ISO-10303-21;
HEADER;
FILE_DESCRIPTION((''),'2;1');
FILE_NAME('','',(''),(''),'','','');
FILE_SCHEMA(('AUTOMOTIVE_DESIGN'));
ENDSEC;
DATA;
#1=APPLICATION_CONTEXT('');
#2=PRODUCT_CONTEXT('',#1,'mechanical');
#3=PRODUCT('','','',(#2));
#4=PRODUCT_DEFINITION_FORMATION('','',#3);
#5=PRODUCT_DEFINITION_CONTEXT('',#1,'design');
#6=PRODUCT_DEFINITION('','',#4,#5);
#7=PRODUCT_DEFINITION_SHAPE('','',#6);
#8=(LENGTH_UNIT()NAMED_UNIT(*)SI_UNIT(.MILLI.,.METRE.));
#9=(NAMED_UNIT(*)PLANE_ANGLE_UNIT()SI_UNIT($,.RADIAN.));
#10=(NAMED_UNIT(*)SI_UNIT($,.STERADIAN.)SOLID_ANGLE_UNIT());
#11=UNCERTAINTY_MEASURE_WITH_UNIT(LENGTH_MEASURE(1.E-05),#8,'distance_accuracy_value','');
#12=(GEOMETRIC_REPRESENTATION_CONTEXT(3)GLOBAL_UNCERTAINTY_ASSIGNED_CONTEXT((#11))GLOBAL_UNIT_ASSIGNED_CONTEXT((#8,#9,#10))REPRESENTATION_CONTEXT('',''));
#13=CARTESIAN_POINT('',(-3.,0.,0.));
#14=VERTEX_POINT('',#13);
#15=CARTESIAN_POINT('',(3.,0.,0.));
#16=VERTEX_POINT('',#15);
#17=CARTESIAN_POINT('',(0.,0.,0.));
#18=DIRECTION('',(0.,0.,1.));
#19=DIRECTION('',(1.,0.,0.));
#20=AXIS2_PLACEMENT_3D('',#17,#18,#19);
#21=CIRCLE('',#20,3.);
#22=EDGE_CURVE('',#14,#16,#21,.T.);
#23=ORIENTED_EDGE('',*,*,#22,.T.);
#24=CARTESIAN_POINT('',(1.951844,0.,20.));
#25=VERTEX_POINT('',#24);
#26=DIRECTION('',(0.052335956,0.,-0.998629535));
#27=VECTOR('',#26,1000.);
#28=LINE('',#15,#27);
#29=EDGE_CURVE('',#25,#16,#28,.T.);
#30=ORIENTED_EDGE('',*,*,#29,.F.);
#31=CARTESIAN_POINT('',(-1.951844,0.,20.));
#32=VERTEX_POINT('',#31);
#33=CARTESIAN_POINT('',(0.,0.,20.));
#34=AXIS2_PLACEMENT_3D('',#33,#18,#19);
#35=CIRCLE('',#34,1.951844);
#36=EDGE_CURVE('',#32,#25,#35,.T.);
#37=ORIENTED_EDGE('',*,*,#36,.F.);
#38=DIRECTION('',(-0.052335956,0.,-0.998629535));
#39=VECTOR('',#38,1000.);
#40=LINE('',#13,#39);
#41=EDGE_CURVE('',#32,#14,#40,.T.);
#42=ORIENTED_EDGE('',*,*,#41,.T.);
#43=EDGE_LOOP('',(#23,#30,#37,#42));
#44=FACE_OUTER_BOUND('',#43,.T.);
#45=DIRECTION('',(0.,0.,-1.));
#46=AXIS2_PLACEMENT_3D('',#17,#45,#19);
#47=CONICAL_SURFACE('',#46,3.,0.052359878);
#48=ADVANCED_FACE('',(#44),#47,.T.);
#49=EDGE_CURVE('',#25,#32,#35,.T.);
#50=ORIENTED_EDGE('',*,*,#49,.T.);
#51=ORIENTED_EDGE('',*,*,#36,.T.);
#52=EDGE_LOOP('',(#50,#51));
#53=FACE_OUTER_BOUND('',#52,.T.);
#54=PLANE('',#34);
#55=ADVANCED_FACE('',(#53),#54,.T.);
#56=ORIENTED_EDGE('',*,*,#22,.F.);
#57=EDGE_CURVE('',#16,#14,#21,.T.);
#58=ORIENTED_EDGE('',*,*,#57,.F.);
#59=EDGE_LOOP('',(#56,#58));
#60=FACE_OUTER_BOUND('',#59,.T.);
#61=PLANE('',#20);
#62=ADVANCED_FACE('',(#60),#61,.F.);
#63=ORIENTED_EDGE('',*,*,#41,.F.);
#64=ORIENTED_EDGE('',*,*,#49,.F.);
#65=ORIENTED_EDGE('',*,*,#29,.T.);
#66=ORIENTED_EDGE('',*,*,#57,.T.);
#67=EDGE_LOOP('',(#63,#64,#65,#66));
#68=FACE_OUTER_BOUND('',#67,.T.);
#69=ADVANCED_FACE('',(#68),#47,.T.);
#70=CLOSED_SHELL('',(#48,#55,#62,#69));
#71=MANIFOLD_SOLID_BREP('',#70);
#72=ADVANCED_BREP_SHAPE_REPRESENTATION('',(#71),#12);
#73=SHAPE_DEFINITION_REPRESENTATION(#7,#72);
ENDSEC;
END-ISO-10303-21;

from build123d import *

# Parameters (mm, degrees)
PIN_PROFILE_6_R                   = 3
TAPER_PIN_BODY_20MM_3_DRAFT_DEPTH = 20
TAPER_PIN_BODY_20MM_3_DRAFT_TAPER = 3


with BuildPart() as part:
    # Pin Profile Ø6 → Taper Pin Body 20mm 3° Draft (new body)
    with BuildSketch(Plane.XY):
        Circle(PIN_PROFILE_6_R)
    extrude(amount=TAPER_PIN_BODY_20MM_3_DRAFT_DEPTH, taper=TAPER_PIN_BODY_20MM_3_DRAFT_TAPER)


solid = part.part
